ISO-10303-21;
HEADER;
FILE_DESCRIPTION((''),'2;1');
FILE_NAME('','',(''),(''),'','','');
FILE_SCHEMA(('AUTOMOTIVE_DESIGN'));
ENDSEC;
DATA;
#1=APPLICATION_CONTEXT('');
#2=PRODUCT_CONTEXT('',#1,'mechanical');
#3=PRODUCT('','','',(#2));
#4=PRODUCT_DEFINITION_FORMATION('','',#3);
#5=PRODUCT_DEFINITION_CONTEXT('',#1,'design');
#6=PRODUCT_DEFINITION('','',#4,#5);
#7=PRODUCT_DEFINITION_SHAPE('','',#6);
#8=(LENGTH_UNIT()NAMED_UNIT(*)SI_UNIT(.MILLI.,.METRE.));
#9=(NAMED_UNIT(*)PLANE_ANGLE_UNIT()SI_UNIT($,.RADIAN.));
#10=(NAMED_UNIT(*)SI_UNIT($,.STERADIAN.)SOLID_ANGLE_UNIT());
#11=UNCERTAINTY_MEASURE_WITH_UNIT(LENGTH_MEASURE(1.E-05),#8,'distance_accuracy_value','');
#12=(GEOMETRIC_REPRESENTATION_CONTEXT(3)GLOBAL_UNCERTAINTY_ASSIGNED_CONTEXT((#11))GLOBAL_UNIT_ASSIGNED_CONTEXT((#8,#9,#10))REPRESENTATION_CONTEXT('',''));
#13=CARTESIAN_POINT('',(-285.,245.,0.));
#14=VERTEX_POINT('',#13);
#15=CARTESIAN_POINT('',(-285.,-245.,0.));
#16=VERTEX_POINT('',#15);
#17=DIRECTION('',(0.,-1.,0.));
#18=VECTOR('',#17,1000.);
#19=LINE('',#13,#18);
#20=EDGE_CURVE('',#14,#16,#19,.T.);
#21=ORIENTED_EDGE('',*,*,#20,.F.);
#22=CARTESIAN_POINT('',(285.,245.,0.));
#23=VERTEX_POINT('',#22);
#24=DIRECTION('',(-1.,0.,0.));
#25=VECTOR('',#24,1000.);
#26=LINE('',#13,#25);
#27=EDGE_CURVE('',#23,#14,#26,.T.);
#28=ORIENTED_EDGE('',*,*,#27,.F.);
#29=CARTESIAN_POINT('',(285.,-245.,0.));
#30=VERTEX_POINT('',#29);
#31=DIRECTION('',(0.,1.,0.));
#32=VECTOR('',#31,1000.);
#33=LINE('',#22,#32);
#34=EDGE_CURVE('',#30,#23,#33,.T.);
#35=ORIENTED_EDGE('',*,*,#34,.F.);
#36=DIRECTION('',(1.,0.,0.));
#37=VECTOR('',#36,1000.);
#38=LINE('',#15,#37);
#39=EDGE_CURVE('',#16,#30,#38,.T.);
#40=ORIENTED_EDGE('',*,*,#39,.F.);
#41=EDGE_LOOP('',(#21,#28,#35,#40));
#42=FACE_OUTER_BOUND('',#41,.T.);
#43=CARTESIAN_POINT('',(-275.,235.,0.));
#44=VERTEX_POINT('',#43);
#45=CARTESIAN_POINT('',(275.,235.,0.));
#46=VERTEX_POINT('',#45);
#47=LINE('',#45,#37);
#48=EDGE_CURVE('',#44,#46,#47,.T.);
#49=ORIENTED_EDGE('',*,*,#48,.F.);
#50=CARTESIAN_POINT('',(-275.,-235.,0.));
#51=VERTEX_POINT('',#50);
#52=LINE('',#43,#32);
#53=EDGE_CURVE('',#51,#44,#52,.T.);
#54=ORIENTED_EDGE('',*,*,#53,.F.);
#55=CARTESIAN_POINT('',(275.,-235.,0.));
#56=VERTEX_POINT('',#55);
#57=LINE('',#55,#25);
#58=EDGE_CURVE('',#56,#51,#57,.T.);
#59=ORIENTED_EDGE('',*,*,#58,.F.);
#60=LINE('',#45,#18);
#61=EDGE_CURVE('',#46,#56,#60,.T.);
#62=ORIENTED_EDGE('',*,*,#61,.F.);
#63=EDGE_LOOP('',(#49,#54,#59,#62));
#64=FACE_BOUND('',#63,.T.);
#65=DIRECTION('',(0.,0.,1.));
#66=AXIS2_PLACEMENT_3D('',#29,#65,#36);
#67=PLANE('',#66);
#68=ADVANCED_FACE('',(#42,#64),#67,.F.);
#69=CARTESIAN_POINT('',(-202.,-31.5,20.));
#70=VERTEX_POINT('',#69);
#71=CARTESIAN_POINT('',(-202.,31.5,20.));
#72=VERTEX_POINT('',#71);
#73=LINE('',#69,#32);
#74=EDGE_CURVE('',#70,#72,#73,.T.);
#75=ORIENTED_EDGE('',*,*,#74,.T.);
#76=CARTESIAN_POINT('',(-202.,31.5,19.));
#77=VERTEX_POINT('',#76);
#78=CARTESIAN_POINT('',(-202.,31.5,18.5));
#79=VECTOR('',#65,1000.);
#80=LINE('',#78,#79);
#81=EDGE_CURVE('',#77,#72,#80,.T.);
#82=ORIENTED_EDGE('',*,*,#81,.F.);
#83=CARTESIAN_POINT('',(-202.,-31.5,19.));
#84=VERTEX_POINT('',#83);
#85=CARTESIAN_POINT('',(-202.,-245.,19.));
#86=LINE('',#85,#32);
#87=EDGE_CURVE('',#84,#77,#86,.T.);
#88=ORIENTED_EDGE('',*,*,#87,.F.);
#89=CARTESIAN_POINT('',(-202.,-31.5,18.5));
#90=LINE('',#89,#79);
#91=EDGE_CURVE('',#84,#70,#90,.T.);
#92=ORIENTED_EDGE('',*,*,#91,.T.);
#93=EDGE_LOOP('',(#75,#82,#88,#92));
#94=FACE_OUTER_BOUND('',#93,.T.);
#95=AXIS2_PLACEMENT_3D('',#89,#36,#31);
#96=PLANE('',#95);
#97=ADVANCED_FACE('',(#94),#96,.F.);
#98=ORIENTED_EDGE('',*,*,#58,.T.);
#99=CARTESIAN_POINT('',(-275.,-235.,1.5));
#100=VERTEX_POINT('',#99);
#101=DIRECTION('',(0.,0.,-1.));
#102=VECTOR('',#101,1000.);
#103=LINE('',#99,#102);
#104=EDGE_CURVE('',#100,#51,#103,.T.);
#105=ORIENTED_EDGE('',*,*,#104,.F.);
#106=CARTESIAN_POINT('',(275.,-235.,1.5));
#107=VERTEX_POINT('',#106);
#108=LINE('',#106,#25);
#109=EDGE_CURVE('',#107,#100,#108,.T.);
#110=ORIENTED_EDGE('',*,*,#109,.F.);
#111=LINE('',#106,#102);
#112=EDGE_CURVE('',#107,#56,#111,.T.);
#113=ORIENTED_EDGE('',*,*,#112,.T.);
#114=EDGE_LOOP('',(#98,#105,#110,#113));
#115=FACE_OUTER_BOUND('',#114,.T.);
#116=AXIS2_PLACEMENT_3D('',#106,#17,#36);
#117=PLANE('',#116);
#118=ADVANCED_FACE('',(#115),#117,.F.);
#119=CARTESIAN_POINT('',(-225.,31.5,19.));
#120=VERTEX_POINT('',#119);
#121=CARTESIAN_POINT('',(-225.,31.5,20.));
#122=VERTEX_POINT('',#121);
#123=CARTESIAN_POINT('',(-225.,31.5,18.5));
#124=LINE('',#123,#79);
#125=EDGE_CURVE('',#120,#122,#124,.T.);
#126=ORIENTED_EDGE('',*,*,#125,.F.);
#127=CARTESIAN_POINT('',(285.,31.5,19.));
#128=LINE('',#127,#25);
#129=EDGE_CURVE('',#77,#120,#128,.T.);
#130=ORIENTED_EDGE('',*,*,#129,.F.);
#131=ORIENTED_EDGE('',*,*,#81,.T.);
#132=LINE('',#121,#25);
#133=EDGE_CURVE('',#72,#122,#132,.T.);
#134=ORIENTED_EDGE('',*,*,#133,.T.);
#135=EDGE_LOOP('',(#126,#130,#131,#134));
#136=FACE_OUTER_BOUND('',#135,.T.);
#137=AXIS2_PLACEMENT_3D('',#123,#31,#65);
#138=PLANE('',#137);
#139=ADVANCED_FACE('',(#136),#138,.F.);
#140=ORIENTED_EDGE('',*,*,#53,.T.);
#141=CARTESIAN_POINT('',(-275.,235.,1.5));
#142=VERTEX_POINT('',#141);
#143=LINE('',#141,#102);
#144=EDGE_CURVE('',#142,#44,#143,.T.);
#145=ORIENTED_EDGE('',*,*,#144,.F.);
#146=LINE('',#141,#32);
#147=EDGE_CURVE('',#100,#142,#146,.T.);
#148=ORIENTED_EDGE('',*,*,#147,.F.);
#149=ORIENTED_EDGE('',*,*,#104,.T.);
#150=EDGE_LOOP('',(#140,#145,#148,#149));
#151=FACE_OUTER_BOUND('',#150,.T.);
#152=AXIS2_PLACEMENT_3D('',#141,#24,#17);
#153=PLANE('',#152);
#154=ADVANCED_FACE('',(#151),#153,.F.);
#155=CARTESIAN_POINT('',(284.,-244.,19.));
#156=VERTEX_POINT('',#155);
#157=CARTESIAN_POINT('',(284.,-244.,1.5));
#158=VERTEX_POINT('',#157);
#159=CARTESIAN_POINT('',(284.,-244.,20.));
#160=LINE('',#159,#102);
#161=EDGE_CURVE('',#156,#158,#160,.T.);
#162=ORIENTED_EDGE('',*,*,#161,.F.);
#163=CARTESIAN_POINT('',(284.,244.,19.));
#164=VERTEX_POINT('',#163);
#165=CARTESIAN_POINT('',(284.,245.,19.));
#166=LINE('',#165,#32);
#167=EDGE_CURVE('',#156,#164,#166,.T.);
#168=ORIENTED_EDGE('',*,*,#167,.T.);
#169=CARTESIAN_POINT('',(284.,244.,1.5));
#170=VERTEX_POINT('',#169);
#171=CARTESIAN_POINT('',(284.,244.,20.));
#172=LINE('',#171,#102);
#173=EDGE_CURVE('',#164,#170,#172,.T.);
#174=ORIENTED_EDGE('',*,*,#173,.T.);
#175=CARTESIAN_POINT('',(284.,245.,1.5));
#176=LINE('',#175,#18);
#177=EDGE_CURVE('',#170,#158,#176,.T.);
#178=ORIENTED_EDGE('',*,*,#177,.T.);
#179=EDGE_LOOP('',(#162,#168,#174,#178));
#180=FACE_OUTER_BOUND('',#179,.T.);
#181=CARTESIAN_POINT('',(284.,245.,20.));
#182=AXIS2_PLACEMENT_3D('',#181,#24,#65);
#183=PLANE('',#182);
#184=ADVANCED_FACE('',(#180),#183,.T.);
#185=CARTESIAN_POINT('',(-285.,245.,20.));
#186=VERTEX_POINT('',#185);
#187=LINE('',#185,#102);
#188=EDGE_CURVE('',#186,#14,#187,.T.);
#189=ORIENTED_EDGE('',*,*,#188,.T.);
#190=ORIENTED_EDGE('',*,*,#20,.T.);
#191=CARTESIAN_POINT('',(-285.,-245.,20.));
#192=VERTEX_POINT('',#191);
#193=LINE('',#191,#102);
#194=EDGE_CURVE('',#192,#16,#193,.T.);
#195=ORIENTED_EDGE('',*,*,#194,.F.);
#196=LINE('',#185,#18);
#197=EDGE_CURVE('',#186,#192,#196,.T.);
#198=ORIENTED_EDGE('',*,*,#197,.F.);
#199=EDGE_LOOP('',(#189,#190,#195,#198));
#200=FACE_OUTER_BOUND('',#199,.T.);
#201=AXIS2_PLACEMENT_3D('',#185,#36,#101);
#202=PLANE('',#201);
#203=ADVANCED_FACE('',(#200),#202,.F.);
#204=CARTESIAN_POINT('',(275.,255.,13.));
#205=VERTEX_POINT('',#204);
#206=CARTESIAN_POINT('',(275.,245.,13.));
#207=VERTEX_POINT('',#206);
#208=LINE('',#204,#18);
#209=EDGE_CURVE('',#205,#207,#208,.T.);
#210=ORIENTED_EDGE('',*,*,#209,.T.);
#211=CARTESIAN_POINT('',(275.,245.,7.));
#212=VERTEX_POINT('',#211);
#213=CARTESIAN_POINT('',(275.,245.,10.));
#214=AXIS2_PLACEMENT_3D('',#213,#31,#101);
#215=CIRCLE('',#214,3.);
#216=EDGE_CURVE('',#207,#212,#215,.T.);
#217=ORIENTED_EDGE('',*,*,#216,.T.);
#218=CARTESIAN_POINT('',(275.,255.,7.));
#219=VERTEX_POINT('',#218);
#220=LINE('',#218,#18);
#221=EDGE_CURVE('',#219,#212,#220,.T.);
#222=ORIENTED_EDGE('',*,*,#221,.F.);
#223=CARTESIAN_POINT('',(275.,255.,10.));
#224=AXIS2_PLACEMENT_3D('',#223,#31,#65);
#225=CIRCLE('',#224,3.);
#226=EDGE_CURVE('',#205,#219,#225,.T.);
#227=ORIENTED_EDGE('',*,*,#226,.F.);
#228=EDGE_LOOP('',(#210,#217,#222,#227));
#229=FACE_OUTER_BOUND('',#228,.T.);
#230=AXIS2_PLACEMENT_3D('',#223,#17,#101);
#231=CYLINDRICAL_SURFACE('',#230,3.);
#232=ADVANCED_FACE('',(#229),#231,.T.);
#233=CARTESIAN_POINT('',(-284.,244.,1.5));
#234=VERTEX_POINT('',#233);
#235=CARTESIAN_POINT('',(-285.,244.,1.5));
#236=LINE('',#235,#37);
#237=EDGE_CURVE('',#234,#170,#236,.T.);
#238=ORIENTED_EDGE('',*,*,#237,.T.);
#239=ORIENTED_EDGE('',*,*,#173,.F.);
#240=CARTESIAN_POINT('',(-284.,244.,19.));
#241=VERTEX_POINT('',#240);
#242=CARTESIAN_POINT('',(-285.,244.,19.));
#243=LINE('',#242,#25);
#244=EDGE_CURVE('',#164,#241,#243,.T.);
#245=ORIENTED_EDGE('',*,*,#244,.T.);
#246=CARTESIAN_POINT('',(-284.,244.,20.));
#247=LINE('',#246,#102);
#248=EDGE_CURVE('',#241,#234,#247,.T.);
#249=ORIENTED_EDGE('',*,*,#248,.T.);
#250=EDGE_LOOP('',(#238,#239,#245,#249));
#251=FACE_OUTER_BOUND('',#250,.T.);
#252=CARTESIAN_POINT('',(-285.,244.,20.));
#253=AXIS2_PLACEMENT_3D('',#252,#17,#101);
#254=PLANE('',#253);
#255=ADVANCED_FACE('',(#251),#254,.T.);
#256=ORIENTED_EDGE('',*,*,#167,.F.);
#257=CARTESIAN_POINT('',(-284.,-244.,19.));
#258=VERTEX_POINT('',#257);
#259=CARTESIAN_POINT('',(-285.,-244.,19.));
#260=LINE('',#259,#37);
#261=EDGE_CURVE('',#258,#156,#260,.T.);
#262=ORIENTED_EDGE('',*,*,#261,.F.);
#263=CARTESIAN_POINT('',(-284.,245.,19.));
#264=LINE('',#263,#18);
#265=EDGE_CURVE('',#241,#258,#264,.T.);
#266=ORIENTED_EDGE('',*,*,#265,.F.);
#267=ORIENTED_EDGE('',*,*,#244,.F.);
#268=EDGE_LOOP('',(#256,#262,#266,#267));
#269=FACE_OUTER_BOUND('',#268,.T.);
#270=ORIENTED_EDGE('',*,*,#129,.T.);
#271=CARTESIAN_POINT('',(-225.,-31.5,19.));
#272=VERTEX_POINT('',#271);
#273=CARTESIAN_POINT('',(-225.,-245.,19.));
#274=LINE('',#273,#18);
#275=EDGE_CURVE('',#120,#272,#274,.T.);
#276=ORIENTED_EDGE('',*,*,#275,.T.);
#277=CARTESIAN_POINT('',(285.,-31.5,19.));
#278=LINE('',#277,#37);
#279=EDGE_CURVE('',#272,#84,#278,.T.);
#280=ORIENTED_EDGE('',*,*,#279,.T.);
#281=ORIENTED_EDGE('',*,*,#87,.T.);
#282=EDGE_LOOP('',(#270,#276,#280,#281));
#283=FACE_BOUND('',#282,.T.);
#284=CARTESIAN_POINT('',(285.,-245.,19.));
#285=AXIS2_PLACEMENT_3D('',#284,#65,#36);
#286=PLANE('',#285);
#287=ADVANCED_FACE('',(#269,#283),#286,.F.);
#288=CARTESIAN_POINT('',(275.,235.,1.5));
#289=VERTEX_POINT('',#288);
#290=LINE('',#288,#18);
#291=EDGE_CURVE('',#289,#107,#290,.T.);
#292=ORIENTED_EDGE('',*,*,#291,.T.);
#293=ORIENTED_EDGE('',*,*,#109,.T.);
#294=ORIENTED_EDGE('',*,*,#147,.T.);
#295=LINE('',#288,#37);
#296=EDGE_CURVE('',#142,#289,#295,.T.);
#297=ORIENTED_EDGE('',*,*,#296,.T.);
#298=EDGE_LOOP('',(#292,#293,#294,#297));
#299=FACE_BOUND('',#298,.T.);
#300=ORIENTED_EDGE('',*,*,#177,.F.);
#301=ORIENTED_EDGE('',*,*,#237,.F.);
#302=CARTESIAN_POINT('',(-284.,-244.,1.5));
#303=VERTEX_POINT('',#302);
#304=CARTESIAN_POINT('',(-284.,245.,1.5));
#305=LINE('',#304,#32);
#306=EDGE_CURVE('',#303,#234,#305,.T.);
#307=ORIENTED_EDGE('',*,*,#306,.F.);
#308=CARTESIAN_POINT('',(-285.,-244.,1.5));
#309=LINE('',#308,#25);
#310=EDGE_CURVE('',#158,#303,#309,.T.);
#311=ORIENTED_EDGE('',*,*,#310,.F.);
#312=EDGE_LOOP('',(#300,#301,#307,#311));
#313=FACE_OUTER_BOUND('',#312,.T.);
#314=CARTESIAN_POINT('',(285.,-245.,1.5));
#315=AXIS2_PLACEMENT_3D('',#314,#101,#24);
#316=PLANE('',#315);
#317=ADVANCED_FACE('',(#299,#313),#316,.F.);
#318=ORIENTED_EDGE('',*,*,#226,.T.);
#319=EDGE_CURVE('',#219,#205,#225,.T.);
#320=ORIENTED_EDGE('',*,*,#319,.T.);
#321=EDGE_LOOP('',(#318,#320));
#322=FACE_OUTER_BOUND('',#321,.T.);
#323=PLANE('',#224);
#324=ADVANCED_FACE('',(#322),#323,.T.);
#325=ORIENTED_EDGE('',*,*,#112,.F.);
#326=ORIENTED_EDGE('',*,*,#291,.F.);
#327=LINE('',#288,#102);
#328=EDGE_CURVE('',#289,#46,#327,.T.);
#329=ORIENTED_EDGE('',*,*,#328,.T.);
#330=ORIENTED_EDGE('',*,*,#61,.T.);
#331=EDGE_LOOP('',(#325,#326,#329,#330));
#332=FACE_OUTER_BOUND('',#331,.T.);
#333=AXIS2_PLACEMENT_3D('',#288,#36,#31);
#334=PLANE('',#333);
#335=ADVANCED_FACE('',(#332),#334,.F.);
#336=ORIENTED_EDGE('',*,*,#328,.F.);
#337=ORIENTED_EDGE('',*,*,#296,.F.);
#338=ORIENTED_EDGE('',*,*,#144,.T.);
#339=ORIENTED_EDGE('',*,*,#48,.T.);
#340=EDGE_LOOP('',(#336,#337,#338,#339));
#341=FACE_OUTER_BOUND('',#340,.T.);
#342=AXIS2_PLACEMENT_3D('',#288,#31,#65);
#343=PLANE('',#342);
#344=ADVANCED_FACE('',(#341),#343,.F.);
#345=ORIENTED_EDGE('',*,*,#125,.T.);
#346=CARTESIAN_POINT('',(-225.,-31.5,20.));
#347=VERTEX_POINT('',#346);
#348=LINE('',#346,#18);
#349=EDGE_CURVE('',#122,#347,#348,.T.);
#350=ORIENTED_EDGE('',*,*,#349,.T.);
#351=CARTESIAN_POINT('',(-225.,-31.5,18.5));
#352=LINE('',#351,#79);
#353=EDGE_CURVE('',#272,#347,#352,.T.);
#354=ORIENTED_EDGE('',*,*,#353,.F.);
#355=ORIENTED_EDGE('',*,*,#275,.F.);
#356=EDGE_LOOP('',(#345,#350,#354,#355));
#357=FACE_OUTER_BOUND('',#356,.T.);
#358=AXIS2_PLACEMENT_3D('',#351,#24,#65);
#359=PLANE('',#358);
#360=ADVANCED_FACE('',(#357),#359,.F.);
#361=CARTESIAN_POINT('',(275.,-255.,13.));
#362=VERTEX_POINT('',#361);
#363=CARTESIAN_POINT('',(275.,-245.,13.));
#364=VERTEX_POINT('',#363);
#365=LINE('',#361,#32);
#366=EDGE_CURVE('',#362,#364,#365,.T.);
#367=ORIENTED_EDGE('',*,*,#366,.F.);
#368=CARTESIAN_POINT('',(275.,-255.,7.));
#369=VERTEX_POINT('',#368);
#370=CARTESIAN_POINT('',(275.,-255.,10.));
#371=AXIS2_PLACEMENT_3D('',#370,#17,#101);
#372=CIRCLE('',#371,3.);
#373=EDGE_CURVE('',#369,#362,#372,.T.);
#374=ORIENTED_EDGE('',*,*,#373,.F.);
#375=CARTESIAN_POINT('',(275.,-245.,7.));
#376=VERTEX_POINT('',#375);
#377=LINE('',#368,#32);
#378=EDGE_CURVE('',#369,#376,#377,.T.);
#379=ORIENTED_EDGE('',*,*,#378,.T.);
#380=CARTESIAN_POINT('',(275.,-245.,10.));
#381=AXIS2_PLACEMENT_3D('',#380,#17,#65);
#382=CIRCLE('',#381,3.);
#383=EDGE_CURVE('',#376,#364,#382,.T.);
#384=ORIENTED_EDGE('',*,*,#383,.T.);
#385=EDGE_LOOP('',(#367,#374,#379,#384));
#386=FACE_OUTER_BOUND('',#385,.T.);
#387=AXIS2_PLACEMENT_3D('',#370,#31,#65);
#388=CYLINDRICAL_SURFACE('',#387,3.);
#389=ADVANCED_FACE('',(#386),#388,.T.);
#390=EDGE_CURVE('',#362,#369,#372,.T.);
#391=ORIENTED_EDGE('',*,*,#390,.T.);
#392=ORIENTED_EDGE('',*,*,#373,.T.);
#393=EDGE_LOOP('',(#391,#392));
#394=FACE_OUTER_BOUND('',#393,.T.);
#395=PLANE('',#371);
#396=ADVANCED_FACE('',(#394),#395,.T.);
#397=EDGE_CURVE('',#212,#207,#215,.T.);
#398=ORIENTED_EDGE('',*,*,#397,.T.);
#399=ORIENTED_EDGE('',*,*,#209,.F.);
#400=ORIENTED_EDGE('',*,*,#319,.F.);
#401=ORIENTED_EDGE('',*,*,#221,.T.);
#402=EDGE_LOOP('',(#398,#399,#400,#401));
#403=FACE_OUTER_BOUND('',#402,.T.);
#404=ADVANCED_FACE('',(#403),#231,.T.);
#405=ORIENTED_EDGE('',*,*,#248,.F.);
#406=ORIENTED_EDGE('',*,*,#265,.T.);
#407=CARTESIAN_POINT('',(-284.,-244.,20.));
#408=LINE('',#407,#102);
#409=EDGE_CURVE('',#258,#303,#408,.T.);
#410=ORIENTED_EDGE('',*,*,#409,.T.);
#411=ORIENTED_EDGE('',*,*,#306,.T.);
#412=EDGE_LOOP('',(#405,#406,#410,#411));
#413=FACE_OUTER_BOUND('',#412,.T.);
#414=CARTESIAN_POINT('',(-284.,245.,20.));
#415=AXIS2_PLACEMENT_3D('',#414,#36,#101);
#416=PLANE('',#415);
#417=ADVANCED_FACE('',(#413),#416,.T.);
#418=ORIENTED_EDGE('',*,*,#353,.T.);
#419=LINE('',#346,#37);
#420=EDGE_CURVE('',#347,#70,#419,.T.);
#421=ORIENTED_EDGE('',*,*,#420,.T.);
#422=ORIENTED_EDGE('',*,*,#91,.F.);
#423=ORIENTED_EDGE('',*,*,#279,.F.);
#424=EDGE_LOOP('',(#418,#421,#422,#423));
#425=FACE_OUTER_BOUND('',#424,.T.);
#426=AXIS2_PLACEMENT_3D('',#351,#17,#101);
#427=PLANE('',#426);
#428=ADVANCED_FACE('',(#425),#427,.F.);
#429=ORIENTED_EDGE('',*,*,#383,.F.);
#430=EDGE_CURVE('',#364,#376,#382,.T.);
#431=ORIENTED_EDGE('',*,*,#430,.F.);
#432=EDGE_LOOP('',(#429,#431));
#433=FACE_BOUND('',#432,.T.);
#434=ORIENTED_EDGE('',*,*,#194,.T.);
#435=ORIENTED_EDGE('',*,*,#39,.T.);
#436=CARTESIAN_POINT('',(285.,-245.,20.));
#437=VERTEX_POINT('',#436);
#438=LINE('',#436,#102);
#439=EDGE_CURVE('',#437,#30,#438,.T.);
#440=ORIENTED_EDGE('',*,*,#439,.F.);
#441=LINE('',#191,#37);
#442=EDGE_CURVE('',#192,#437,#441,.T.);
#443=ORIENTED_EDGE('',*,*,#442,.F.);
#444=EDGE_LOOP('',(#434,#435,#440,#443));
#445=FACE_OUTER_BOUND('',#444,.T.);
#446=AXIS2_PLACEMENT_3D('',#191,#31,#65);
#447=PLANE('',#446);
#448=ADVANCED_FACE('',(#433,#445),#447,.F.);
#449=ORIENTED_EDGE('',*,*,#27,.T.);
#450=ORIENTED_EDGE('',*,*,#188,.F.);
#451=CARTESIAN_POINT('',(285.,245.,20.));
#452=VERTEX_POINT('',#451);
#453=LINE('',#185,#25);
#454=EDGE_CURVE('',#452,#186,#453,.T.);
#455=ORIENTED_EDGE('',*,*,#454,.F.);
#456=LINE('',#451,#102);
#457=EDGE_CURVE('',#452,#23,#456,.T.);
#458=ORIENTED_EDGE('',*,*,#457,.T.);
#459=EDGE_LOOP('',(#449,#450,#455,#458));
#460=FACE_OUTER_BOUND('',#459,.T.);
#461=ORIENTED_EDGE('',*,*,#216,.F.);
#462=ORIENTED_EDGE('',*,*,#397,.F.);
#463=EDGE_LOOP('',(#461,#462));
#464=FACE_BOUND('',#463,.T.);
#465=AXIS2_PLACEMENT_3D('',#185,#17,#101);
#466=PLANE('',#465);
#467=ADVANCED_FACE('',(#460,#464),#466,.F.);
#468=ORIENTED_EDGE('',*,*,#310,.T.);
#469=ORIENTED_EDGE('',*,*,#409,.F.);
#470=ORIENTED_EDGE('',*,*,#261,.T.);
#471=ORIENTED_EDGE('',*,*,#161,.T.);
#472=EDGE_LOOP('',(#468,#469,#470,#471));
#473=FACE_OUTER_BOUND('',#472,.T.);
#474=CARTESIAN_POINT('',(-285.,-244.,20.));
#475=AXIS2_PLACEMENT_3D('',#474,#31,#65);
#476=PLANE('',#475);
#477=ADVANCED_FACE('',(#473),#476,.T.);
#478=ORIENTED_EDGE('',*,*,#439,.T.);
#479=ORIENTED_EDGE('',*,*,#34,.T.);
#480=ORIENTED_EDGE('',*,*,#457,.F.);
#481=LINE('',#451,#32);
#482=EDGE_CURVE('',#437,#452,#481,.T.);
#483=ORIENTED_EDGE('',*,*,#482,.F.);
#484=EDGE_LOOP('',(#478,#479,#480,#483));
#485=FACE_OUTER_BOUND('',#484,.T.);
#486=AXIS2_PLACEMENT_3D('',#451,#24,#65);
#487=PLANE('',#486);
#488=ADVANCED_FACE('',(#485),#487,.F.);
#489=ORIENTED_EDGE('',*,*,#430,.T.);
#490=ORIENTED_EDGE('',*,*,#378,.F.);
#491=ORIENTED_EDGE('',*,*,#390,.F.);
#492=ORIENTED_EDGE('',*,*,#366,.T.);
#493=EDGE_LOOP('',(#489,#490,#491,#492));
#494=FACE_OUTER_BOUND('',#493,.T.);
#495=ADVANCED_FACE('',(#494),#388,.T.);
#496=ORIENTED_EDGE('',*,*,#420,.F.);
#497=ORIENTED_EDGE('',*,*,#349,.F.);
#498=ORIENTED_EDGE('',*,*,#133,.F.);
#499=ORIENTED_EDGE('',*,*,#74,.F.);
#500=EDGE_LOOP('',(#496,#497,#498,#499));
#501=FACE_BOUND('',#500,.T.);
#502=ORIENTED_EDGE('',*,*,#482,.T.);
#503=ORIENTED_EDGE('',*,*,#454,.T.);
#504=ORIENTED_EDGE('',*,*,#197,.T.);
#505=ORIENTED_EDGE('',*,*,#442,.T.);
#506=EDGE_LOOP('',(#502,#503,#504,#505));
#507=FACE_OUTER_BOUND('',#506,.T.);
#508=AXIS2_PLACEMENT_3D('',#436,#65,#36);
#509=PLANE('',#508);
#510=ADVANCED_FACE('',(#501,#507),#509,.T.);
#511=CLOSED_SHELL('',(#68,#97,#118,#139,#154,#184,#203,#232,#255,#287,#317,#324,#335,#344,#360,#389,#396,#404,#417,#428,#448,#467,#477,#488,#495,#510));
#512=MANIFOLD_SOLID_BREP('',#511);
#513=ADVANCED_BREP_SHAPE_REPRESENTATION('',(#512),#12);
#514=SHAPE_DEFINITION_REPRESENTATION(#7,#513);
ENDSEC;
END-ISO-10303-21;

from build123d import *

# Parameters (mm, degrees)
SKETCH_1_W          = 570
SKETCH_1_H          = 490
EXTRUDE_1_DEPTH     = 20
SHELL_3_T           = -1
SKETCH_5_W          = 570
SKETCH_5_H          = 490
SKETCH_5_W_2        = 550
SKETCH_5_H_2        = 470
EXTRUDE_3_DEPTH     = 1.5
SKETCH_11_R         = 3
EXTRUDE_4_DEPTH     = 10
EXTRUDE_START       = 10
SKETCH_12_R         = 3
EXTRUDE_5_DEPTH     = 10
SKETCH_13_W         = 23
SKETCH_13_H         = 63
CUT_EXTRUDE_3_DEPTH = 1.5


with BuildPart() as part:
    # 草图1 → 凸台-拉伸1 (new body)
    with BuildSketch(Plane.XY):
        Rectangle(SKETCH_1_W, SKETCH_1_H)
    extrude(amount=EXTRUDE_1_DEPTH)

    # 抽壳3
    shell_3_openings = [part.faces().sort_by_distance(p)[0] for p in [
        (0, 0, 0),
    ]]
    offset(amount=SHELL_3_T, openings=shell_3_openings, kind=Kind.INTERSECTION)

    # 草图5 → 凸台-拉伸3 (add)
    with BuildSketch(Plane(origin=(0, 0, 0), x_dir=(-1, 0, 0), z_dir=(0, 0, -1))):
        Rectangle(SKETCH_5_W, SKETCH_5_H)
        Rectangle(SKETCH_5_W_2, SKETCH_5_H_2, mode=Mode.SUBTRACT)
    extrude(amount=-EXTRUDE_3_DEPTH)

    # 草图11 → 凸台-拉伸4 (add)
    with BuildSketch(Plane(origin=(0, 245, 0), x_dir=(1, 0, 0), z_dir=(0, 1, 0))):
        with Locations(Location((275, -10, 0), (0, 0, 90))):
            Circle(SKETCH_11_R)
    extrude(amount=EXTRUDE_4_DEPTH)

    # 草图12 → 凸台-拉伸5 (add)
    with BuildSketch(Plane.XZ.offset(245).offset(EXTRUDE_START)):
        with Locations(Location((275, 10, 0), (0, 0, 270))):
            Circle(SKETCH_12_R)
    extrude(amount=-EXTRUDE_5_DEPTH)

    # 草图13 → 切除-拉伸3 (cut)
    with BuildSketch(Plane.XY.offset(20)):
        with Locations((-213.5, 0)):
            Rectangle(SKETCH_13_W, SKETCH_13_H)
    extrude(amount=-CUT_EXTRUDE_3_DEPTH, mode=Mode.SUBTRACT)


solid = part.part
